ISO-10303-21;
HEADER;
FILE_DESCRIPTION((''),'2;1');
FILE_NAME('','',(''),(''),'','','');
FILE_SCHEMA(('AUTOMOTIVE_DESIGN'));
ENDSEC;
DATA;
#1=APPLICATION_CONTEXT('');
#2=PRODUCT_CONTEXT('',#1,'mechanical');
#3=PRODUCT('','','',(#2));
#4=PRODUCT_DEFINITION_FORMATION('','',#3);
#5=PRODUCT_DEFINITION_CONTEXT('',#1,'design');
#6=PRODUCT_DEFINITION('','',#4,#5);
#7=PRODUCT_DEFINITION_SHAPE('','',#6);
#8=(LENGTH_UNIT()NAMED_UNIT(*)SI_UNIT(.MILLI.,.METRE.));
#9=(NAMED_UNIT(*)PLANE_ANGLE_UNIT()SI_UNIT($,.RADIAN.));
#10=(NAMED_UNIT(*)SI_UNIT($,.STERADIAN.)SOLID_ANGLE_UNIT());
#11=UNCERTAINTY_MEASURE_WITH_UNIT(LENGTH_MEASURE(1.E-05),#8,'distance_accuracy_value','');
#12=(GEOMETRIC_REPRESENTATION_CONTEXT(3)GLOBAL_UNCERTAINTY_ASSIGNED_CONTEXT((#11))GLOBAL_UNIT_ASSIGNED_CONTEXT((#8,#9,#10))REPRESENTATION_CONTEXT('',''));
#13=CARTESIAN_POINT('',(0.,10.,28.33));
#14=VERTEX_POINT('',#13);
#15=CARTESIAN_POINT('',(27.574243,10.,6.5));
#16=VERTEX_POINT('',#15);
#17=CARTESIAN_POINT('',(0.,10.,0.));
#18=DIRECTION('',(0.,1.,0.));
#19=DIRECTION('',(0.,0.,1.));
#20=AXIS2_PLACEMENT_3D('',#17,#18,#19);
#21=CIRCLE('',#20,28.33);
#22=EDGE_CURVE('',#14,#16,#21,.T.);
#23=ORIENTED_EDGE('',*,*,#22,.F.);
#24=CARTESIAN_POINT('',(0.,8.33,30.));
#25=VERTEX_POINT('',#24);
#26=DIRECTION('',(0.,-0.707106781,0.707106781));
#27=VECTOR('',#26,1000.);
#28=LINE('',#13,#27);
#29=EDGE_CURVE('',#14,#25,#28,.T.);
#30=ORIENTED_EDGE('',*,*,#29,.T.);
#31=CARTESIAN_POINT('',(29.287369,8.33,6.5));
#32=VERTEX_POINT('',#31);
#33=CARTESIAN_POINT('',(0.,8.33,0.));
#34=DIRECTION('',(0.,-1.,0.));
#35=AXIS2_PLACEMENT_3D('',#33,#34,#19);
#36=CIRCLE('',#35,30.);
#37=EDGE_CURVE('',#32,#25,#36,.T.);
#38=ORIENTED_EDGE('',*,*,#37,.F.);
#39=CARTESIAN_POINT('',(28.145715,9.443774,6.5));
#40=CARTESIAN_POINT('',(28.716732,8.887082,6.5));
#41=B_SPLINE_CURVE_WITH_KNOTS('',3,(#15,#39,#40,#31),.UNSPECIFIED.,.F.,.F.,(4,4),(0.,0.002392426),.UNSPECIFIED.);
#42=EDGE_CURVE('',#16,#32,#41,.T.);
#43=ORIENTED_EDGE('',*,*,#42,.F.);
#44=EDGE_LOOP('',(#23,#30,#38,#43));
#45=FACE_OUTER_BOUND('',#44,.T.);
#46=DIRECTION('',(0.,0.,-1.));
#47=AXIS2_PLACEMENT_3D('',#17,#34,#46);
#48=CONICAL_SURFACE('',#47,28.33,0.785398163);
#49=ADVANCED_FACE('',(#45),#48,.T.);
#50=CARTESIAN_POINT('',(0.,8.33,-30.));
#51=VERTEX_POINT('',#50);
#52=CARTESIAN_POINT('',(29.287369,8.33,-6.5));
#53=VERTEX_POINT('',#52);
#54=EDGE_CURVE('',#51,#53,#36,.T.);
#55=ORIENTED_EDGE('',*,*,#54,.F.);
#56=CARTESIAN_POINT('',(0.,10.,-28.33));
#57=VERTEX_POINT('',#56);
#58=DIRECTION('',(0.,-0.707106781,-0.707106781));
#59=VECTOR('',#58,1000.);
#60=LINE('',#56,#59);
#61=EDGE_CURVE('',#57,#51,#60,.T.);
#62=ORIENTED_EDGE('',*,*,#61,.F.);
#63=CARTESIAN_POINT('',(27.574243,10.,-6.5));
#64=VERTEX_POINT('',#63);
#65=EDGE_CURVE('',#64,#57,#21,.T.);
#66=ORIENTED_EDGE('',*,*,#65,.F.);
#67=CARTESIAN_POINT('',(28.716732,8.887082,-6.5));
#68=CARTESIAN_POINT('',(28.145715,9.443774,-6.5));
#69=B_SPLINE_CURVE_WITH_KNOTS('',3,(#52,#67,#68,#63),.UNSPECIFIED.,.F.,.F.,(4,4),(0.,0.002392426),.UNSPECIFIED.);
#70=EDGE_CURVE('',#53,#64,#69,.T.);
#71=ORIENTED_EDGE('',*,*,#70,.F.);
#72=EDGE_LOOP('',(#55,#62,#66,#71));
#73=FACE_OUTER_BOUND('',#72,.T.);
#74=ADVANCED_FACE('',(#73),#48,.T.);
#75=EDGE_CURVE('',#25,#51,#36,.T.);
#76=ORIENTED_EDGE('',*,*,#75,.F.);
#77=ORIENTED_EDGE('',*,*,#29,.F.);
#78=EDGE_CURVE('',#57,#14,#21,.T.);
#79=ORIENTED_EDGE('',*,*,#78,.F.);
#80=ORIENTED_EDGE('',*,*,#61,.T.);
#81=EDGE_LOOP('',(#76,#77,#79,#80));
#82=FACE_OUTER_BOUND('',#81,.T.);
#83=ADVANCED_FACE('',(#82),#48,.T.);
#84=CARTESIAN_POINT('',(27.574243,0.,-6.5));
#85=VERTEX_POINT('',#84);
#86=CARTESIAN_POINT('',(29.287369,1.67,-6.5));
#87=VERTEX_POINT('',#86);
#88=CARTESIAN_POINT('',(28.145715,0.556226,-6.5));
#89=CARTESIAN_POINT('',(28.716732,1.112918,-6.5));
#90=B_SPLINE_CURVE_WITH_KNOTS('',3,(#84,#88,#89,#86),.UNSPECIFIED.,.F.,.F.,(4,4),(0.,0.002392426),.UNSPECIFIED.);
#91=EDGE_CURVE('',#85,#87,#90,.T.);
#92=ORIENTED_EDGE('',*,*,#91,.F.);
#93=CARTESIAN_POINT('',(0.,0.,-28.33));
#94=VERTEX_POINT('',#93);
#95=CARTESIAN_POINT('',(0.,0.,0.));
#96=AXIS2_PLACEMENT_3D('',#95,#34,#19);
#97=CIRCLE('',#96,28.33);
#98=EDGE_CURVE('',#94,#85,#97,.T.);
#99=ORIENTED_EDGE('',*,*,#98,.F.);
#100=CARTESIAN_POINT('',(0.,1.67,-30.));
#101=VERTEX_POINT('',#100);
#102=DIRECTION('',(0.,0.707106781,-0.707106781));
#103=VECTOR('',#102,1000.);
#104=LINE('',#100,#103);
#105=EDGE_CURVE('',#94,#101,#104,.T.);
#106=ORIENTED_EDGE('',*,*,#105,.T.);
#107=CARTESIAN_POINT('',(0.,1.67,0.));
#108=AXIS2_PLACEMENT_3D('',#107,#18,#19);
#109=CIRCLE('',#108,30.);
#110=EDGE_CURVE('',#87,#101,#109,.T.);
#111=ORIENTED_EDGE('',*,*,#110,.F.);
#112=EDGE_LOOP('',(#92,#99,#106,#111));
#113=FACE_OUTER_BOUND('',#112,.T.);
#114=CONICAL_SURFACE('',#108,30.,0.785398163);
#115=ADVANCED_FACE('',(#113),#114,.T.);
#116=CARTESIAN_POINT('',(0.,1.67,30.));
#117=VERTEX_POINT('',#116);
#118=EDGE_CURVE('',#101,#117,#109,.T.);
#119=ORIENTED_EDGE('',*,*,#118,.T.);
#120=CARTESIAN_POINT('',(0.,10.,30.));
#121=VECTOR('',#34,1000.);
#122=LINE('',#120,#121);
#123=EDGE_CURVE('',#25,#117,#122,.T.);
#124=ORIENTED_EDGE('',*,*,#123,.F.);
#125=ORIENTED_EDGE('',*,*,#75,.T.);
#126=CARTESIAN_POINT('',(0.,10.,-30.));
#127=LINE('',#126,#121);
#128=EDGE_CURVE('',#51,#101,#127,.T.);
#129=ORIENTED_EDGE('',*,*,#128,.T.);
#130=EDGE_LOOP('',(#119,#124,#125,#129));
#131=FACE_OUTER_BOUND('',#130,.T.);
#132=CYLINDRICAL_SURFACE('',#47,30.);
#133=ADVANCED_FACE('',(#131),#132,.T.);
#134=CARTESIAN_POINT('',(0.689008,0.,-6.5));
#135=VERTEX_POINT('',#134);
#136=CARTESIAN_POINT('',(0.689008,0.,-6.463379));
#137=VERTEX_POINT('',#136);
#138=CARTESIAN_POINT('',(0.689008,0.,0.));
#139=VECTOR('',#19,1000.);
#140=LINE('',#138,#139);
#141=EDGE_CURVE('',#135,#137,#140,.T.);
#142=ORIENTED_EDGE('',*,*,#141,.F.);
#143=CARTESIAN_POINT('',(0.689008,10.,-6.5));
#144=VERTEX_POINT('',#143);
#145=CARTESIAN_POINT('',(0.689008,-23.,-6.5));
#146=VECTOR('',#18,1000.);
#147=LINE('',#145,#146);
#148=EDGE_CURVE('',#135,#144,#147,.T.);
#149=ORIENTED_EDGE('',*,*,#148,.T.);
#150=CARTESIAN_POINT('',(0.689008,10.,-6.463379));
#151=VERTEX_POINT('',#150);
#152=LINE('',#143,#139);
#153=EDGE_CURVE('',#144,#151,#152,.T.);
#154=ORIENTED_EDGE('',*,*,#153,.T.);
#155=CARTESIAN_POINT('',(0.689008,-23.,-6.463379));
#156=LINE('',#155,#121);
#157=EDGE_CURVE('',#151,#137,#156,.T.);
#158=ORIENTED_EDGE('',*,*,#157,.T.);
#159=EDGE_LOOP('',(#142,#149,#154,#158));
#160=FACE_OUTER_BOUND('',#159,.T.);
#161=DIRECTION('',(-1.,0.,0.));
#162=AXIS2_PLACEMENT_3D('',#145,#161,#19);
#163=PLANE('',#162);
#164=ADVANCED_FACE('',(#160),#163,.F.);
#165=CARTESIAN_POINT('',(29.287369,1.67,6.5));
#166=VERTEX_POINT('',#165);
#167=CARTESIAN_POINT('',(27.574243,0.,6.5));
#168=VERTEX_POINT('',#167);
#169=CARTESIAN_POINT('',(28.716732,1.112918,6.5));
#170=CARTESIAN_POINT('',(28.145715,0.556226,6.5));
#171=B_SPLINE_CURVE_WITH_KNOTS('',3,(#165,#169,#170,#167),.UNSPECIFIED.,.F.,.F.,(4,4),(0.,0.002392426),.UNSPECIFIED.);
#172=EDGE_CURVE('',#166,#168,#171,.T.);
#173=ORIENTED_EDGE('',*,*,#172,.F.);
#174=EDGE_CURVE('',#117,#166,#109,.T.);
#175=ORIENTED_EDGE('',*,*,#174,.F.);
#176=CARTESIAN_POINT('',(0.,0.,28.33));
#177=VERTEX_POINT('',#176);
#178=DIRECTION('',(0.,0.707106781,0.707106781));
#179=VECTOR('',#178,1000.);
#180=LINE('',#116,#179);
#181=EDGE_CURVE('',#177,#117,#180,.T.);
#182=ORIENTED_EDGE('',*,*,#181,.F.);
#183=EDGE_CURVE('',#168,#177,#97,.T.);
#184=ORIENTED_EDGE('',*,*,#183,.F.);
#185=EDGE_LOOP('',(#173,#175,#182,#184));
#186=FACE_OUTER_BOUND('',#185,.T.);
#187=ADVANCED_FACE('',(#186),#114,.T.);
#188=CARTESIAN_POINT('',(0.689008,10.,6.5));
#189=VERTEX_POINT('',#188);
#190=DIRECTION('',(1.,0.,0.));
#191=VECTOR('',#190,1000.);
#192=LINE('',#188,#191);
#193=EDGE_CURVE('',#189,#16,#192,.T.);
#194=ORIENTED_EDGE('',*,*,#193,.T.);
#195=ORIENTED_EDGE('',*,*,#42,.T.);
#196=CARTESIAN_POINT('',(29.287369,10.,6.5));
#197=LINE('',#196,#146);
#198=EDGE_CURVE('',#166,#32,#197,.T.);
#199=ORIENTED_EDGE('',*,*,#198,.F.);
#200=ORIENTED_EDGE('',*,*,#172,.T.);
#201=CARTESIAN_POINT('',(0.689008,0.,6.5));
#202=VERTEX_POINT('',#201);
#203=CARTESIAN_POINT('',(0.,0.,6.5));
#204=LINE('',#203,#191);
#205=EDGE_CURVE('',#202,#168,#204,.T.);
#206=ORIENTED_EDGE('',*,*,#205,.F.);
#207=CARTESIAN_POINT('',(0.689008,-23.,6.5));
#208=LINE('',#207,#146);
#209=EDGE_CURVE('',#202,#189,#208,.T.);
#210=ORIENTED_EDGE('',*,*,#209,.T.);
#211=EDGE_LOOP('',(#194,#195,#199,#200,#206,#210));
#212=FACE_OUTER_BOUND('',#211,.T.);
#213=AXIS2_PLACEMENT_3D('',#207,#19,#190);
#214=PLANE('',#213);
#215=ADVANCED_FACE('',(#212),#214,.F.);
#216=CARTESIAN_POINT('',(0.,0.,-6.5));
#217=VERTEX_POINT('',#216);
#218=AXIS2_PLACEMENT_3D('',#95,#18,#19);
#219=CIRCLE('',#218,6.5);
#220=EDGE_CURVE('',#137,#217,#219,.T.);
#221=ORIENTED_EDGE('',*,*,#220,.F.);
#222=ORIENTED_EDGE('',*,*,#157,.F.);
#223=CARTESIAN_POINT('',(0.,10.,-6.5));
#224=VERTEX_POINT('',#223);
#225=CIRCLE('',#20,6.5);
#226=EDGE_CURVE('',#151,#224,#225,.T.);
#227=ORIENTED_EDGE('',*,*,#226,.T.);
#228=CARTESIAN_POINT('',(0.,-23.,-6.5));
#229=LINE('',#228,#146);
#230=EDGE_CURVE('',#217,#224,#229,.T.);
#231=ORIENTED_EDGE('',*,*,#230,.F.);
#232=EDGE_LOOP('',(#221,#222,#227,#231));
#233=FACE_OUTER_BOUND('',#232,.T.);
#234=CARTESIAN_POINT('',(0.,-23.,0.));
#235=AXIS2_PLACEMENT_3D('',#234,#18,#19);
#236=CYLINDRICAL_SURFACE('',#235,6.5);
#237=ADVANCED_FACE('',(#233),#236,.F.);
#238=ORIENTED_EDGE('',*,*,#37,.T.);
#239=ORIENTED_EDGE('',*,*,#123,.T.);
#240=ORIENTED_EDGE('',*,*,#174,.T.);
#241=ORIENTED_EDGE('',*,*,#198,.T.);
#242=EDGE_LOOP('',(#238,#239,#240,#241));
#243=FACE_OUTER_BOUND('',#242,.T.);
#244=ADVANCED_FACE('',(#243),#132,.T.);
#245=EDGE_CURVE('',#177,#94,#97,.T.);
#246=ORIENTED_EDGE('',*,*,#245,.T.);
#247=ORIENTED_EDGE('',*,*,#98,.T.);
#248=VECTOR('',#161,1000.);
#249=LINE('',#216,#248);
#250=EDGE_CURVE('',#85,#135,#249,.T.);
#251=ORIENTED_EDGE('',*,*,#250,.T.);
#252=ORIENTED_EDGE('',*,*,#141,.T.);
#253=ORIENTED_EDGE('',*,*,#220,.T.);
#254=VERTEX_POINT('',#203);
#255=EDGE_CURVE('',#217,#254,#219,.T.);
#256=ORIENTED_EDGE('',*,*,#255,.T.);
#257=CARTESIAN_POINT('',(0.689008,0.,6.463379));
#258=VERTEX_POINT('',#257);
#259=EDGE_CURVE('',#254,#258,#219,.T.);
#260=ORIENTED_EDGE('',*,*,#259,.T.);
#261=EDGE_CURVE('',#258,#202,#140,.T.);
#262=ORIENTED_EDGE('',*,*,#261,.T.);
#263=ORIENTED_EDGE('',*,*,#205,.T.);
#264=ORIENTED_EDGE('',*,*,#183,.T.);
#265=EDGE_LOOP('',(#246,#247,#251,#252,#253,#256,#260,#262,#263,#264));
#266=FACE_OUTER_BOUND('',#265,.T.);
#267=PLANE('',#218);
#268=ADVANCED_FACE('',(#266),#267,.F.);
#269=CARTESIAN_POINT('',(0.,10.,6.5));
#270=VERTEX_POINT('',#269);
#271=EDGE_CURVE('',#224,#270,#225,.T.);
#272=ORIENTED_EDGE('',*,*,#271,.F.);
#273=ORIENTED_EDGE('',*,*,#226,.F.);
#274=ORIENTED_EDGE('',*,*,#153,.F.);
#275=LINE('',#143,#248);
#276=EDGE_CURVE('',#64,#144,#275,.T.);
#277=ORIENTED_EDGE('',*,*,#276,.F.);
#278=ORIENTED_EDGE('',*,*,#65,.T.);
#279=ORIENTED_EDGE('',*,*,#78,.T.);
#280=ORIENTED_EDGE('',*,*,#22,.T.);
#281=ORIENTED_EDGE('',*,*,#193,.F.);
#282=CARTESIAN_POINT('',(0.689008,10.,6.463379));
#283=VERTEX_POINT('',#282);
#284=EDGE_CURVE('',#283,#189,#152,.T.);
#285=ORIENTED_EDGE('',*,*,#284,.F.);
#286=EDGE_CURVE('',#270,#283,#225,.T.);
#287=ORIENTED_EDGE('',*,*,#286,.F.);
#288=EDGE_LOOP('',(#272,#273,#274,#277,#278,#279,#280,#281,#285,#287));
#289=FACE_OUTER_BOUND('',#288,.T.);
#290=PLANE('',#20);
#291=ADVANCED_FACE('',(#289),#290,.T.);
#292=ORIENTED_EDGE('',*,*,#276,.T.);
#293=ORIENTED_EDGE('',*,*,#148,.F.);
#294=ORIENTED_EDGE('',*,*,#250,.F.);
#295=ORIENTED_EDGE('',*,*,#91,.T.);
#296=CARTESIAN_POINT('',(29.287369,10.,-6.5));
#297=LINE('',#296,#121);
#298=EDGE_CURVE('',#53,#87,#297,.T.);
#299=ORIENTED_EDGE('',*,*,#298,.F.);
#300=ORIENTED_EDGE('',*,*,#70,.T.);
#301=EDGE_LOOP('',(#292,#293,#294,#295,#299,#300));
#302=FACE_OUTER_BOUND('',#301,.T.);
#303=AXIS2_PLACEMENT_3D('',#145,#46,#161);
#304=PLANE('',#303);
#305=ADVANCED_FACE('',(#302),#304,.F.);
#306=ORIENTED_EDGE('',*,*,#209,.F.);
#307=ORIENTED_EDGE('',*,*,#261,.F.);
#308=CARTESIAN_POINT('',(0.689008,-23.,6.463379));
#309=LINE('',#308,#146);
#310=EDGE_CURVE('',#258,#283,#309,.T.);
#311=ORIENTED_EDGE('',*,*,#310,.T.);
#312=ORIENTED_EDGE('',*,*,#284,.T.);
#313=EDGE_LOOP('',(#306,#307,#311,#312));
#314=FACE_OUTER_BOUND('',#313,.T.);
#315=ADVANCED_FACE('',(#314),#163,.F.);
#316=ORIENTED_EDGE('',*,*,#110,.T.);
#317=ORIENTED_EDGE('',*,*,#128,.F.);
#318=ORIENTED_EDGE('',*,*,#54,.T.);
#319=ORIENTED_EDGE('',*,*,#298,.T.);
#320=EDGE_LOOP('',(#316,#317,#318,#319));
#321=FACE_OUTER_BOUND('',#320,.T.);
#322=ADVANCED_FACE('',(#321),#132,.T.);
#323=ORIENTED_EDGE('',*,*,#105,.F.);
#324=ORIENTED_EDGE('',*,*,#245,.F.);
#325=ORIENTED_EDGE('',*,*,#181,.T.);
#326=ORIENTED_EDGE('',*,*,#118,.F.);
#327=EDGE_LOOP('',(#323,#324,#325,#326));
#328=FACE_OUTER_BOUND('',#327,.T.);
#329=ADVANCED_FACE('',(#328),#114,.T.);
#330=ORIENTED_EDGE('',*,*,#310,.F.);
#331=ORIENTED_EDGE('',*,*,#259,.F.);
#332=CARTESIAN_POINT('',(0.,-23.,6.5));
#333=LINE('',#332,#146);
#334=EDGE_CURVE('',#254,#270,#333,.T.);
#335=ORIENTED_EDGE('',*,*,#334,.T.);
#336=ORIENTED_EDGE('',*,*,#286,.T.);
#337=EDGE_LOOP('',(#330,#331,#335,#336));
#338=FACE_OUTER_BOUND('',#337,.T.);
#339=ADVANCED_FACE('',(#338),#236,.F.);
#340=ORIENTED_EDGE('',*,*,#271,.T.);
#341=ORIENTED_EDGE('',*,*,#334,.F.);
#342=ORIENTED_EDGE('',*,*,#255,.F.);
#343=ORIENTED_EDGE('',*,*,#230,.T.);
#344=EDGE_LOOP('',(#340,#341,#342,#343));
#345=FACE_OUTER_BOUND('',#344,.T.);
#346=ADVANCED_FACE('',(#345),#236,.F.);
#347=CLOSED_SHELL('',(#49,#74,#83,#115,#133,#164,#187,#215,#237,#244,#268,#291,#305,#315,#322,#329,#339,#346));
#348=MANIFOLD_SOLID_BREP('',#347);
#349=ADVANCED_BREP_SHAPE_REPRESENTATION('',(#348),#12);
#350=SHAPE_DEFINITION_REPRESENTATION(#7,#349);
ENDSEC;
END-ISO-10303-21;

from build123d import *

# Parameters (mm, degrees)
SKETCH1_R           = 30
BOSS_EXTRUDE1_DEPTH = 10
SKETCH2_W           = 58.621984262
SKETCH2_H           = 13
CUT_EXTRUDE1_DEPTH  = 33
SKETCH3_R           = 6.5
CUT_EXTRUDE2_DEPTH  = 33
CHAMFER1_SIZE       = 1.67


with BuildPart() as part:
    # Sketch1 → Boss-Extrude1 (new body)
    with BuildSketch(Plane(origin=(0, 0, 0), x_dir=(1, 0, 0), z_dir=(0, 1, 0))):
        with Locations(Location((0, 0, 0), (0, 0, 270))):
            Circle(SKETCH1_R)
    extrude(amount=BOSS_EXTRUDE1_DEPTH)

    # Sketch2 → Cut-Extrude1 (cut)
    with BuildSketch(Plane(origin=(0, 10, 0), x_dir=(1, 0, 0), z_dir=(0, 1, 0))):
        with Locations((30, 0)):
            Rectangle(SKETCH2_W, SKETCH2_H)
    extrude(amount=-CUT_EXTRUDE1_DEPTH, mode=Mode.SUBTRACT)

    # Sketch3 → Cut-Extrude2 (cut)
    with BuildSketch(Plane(origin=(0, 10, 0), x_dir=(1, 0, 0), z_dir=(0, 1, 0))):
        Circle(SKETCH3_R)
    extrude(amount=-CUT_EXTRUDE2_DEPTH, mode=Mode.SUBTRACT)

    # Chamfer1
    chamfer1_edges = [part.edges().sort_by_distance(p)[0] for p in [
        (-30, 0, 0),
        (-30, 10, 0),
    ]]
    chamfer(chamfer1_edges, length=CHAMFER1_SIZE)


solid = part.part
